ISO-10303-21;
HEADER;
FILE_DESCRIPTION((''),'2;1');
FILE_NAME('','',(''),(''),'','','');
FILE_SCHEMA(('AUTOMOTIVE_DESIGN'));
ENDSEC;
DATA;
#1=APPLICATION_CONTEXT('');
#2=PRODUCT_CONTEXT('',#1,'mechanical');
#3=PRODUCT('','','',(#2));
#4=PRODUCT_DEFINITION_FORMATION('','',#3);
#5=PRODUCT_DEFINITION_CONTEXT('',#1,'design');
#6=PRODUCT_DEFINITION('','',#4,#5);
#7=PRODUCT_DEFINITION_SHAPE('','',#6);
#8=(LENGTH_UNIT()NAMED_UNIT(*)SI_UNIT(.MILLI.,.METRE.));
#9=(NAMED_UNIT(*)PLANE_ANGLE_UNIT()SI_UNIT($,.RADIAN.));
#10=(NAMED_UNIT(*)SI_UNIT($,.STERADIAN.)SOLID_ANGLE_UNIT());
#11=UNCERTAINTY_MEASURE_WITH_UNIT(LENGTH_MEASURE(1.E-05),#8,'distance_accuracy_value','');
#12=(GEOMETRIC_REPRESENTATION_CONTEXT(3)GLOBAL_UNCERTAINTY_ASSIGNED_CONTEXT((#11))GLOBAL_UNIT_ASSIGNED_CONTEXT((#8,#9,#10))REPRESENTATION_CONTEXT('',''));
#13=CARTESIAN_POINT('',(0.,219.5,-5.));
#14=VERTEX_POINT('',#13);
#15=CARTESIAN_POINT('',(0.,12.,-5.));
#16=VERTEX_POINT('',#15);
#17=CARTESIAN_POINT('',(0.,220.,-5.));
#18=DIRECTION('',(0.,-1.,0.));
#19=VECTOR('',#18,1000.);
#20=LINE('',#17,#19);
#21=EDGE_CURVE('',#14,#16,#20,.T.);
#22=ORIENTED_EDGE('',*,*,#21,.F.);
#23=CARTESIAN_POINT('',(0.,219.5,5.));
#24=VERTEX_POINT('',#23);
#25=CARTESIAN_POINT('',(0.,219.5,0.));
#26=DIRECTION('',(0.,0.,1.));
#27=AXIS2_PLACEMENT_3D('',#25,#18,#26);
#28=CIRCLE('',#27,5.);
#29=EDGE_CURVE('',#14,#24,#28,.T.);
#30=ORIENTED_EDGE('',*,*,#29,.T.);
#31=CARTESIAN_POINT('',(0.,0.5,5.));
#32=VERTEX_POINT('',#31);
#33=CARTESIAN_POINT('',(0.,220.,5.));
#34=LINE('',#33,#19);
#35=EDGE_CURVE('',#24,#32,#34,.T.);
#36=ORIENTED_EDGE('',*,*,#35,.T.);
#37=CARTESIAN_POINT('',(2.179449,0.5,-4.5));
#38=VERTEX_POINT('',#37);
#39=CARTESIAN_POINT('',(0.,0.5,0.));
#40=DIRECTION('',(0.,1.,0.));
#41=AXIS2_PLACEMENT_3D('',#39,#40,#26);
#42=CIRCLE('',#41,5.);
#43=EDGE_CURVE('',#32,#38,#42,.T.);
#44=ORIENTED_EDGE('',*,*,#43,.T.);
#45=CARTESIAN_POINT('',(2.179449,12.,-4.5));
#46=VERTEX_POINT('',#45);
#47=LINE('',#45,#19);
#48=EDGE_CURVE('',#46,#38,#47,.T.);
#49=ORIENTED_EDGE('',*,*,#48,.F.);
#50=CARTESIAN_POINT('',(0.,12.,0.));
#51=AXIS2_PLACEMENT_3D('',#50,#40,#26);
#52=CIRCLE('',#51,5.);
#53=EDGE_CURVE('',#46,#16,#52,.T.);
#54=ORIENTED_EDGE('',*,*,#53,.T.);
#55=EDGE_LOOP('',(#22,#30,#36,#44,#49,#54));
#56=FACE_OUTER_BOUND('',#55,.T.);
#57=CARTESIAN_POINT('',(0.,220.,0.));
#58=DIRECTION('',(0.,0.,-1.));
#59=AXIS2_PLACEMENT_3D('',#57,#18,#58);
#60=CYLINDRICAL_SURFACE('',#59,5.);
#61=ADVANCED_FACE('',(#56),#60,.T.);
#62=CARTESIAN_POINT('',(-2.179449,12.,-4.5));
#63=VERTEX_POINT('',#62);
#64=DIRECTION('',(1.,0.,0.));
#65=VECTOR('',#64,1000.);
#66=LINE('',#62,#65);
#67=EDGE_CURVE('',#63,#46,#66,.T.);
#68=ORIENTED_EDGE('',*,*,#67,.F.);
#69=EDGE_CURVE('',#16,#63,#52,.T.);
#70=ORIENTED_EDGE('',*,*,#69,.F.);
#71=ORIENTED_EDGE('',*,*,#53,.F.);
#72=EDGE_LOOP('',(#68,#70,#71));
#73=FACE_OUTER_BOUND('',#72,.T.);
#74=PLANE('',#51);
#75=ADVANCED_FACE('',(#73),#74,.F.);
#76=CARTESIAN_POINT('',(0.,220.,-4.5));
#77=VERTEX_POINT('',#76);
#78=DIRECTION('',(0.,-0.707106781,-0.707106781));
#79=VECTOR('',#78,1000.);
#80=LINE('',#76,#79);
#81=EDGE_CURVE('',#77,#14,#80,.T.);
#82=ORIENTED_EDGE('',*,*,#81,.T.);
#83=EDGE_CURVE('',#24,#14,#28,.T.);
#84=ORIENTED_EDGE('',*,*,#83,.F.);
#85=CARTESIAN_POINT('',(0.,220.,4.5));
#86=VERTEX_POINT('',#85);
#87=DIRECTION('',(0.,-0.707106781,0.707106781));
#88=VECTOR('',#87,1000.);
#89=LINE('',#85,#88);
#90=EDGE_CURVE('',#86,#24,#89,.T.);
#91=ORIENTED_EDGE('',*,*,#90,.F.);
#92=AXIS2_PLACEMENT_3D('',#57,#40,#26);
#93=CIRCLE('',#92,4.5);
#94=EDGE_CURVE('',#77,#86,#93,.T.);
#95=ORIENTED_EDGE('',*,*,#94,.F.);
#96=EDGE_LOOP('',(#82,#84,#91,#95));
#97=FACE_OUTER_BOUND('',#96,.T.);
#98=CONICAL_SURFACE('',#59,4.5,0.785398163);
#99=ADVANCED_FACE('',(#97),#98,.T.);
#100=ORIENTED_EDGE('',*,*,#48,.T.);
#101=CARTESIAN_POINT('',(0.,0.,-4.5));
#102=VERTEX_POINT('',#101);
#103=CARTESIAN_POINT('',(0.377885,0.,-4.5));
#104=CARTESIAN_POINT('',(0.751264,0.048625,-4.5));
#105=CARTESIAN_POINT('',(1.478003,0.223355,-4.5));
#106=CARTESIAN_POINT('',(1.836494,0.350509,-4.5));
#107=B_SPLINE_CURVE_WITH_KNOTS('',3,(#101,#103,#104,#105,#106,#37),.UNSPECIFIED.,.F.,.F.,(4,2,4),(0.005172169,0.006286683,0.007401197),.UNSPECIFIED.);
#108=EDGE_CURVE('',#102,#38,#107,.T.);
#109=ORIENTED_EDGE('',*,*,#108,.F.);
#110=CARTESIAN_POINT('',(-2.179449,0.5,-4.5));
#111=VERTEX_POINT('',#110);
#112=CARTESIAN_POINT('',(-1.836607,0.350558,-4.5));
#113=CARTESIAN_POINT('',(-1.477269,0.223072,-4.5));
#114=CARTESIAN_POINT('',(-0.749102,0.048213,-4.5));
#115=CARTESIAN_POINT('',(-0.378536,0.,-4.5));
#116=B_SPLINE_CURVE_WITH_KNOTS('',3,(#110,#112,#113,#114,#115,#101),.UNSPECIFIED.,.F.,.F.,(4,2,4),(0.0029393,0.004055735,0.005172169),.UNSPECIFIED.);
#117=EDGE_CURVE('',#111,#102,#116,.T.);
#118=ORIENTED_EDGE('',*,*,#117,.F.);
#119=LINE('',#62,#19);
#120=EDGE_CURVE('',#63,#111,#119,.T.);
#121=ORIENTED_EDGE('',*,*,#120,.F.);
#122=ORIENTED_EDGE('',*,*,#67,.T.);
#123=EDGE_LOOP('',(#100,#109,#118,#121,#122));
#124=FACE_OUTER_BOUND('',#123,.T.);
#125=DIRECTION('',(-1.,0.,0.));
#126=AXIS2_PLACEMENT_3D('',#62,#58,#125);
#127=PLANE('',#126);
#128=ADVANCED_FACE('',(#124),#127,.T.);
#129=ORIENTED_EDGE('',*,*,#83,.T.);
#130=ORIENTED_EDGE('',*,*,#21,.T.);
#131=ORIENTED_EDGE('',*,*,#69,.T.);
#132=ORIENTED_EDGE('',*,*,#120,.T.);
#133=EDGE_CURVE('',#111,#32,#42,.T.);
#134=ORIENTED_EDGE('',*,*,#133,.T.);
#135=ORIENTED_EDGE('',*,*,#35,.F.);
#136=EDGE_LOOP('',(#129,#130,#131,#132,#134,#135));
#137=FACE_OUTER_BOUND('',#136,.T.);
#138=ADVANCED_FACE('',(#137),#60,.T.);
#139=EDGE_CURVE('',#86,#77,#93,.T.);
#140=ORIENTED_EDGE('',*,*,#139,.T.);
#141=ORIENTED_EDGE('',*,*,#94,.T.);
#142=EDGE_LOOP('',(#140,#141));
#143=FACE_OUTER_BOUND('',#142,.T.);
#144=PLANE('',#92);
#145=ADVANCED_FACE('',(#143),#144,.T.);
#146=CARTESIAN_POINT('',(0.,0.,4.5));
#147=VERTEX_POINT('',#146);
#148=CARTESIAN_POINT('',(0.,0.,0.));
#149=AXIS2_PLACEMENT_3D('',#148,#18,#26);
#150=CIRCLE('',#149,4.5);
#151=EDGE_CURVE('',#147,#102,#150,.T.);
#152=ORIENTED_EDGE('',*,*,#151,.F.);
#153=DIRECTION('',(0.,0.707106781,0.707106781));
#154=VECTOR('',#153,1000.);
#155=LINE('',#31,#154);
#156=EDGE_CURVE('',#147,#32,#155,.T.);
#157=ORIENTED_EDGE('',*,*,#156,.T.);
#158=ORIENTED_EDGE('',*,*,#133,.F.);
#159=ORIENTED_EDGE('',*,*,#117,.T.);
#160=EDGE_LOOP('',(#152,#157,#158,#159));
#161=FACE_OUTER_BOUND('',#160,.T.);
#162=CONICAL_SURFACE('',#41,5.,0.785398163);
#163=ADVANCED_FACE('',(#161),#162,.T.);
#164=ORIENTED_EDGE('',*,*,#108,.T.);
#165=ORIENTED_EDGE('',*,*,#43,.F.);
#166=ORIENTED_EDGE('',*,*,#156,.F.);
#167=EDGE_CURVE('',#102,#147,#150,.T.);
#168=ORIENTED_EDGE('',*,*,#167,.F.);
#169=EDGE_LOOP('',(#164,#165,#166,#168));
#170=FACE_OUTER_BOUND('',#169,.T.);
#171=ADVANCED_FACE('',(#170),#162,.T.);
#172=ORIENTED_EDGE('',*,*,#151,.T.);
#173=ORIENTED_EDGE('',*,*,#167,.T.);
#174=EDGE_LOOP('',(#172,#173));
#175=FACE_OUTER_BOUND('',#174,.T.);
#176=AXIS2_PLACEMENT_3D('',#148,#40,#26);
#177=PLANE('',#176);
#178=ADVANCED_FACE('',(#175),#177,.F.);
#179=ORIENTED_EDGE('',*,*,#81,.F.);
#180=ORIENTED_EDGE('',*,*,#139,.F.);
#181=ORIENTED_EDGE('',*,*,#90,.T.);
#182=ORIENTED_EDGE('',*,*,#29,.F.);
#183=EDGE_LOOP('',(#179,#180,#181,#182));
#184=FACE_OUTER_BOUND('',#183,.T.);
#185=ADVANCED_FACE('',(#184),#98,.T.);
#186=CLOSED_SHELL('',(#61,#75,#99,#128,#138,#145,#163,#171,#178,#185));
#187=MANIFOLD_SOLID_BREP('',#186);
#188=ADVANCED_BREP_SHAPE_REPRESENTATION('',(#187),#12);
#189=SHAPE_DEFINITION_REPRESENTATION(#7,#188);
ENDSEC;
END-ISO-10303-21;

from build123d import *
from build123d.topology import SkipClean

# Parameters (mm, degrees)
SKETCH1_R           = 5
BOSS_EXTRUDE1_DEPTH = 220
CHAMFER1_SIZE       = 0.5
CUT_EXTRUDE1_DEPTH  = 12


with BuildPart() as part:
    # Sketch1 → Boss-Extrude1 (new body)
    with BuildSketch(Plane(origin=(0, 0, 0), x_dir=(1, 0, 0), z_dir=(0, 1, 0))):
        with Locations(Location((0, 0, 0), (0, 0, 270))):
            Circle(SKETCH1_R)
    extrude(amount=BOSS_EXTRUDE1_DEPTH)

    # Chamfer1
    chamfer1_edges = [part.edges().sort_by_distance(p)[0] for p in [
        (0, 0, -5),
        (0, 220, -5),
    ]]
    chamfer(chamfer1_edges, length=CHAMFER1_SIZE)

    # Sketch2 → Cut-Extrude1 (cut)
    with SkipClean():  # the faces are left unmerged after this step: merging them gives an invalid solid
        with BuildSketch(Plane(origin=(0, 0, 0), x_dir=(1, 0, 0), z_dir=(0, 1, 0))):
            with BuildLine():
                Line((-2.179449472, 4.5), (2.179449472, 4.5))
                ThreePointArc((2.179449472, 4.5), (0, 5), (-2.179449472, 4.5))
            make_face()
        extrude(amount=CUT_EXTRUDE1_DEPTH, mode=Mode.SUBTRACT)


solid = part.part
